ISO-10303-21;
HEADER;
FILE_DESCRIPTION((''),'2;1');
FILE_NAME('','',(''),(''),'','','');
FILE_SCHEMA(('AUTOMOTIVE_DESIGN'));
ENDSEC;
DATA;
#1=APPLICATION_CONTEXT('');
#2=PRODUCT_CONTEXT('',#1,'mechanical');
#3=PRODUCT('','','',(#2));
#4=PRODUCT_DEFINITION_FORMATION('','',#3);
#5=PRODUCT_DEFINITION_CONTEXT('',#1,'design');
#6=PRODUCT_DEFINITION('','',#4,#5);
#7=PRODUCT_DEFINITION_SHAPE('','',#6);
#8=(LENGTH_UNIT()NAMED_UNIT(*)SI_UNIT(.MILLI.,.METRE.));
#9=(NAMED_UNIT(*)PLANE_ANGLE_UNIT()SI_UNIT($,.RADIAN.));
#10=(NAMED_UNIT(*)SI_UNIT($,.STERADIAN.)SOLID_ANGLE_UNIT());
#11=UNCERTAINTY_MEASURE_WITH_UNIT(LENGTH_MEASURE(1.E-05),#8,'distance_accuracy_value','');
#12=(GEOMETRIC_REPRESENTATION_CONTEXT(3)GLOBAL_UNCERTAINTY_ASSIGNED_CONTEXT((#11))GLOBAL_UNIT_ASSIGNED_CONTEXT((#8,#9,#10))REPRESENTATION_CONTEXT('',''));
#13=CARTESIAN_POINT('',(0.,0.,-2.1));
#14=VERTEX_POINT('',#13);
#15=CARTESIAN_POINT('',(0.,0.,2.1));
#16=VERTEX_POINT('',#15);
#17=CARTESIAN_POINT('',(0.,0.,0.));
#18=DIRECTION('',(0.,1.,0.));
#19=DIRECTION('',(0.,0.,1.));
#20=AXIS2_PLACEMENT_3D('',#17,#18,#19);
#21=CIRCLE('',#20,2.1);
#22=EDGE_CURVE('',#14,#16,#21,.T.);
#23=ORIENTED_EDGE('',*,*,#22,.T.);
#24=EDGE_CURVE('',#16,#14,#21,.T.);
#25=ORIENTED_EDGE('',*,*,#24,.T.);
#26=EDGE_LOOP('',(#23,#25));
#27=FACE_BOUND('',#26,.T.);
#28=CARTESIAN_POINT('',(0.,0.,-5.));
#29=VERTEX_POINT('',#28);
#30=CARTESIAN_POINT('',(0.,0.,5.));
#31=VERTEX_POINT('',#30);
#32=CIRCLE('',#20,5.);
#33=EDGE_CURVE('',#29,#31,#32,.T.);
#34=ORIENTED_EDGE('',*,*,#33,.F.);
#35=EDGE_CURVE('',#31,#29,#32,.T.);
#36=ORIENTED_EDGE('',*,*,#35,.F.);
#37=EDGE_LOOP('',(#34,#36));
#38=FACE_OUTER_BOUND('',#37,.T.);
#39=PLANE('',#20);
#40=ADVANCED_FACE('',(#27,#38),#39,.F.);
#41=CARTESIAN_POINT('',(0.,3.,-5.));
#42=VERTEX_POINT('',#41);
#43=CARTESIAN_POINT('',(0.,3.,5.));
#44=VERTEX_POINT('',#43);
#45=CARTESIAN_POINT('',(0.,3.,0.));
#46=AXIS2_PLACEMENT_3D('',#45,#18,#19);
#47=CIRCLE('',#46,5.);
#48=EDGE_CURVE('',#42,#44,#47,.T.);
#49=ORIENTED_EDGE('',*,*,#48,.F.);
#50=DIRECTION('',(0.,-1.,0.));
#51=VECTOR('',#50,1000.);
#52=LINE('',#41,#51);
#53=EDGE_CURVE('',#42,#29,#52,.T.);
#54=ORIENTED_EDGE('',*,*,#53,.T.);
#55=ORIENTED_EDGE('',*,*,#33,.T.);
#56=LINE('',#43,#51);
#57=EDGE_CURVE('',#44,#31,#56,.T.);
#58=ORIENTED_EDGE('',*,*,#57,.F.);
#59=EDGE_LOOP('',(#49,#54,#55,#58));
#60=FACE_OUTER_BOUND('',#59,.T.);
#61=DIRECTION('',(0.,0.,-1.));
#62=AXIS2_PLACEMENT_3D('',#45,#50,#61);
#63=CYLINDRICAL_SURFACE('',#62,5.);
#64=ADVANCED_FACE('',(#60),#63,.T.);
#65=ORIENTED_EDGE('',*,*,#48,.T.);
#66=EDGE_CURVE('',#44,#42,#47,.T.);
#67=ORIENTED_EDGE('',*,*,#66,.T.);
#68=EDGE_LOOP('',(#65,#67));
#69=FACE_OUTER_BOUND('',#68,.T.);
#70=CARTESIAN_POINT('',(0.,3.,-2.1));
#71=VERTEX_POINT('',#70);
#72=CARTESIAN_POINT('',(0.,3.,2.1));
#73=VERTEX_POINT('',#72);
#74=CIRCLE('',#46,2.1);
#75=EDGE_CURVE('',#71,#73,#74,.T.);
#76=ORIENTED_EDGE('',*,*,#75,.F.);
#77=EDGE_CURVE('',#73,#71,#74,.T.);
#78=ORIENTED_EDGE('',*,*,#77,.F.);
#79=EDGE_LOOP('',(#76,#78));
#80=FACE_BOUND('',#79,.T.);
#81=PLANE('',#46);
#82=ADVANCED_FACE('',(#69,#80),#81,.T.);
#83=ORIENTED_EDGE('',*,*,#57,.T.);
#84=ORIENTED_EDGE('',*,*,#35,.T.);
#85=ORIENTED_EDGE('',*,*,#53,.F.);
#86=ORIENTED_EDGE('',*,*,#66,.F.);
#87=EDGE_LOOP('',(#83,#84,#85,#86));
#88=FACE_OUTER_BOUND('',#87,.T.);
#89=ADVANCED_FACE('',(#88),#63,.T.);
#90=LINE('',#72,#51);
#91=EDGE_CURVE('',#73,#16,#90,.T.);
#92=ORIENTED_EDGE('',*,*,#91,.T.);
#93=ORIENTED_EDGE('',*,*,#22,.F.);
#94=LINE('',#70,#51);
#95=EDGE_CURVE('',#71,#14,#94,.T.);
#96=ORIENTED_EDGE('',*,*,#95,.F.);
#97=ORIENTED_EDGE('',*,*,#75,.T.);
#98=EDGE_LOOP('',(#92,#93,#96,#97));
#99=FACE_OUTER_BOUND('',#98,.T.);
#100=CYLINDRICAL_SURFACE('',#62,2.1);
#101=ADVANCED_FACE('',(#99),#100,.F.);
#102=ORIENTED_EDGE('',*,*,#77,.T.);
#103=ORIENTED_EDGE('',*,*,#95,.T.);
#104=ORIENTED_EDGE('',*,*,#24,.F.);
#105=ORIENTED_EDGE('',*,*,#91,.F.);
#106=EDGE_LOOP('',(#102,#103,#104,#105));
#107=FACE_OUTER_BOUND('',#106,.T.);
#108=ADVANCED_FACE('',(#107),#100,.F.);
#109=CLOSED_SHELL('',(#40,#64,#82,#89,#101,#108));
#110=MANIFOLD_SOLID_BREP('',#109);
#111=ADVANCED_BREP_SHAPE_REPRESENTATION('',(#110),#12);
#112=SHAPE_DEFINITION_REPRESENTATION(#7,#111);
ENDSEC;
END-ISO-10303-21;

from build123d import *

# Parameters (mm, degrees)
SKETCH_1_R      = 5
SKETCH_1_R_2    = 2.1
EXTRUDE_1_DEPTH = 3


with BuildPart() as part:
    # 草图1 → 凸台-拉伸1 (new body)
    with BuildSketch(Plane(origin=(0, 0, 0), x_dir=(1, 0, 0), z_dir=(0, 1, 0))):
        with Locations(Location((0, 0, 0), (0, 0, 270))):
            Circle(SKETCH_1_R)
        with Locations(Location((0, 0, 0), (0, 0, 270))):
            Circle(SKETCH_1_R_2, mode=Mode.SUBTRACT)
    extrude(amount=EXTRUDE_1_DEPTH)


solid = part.part
